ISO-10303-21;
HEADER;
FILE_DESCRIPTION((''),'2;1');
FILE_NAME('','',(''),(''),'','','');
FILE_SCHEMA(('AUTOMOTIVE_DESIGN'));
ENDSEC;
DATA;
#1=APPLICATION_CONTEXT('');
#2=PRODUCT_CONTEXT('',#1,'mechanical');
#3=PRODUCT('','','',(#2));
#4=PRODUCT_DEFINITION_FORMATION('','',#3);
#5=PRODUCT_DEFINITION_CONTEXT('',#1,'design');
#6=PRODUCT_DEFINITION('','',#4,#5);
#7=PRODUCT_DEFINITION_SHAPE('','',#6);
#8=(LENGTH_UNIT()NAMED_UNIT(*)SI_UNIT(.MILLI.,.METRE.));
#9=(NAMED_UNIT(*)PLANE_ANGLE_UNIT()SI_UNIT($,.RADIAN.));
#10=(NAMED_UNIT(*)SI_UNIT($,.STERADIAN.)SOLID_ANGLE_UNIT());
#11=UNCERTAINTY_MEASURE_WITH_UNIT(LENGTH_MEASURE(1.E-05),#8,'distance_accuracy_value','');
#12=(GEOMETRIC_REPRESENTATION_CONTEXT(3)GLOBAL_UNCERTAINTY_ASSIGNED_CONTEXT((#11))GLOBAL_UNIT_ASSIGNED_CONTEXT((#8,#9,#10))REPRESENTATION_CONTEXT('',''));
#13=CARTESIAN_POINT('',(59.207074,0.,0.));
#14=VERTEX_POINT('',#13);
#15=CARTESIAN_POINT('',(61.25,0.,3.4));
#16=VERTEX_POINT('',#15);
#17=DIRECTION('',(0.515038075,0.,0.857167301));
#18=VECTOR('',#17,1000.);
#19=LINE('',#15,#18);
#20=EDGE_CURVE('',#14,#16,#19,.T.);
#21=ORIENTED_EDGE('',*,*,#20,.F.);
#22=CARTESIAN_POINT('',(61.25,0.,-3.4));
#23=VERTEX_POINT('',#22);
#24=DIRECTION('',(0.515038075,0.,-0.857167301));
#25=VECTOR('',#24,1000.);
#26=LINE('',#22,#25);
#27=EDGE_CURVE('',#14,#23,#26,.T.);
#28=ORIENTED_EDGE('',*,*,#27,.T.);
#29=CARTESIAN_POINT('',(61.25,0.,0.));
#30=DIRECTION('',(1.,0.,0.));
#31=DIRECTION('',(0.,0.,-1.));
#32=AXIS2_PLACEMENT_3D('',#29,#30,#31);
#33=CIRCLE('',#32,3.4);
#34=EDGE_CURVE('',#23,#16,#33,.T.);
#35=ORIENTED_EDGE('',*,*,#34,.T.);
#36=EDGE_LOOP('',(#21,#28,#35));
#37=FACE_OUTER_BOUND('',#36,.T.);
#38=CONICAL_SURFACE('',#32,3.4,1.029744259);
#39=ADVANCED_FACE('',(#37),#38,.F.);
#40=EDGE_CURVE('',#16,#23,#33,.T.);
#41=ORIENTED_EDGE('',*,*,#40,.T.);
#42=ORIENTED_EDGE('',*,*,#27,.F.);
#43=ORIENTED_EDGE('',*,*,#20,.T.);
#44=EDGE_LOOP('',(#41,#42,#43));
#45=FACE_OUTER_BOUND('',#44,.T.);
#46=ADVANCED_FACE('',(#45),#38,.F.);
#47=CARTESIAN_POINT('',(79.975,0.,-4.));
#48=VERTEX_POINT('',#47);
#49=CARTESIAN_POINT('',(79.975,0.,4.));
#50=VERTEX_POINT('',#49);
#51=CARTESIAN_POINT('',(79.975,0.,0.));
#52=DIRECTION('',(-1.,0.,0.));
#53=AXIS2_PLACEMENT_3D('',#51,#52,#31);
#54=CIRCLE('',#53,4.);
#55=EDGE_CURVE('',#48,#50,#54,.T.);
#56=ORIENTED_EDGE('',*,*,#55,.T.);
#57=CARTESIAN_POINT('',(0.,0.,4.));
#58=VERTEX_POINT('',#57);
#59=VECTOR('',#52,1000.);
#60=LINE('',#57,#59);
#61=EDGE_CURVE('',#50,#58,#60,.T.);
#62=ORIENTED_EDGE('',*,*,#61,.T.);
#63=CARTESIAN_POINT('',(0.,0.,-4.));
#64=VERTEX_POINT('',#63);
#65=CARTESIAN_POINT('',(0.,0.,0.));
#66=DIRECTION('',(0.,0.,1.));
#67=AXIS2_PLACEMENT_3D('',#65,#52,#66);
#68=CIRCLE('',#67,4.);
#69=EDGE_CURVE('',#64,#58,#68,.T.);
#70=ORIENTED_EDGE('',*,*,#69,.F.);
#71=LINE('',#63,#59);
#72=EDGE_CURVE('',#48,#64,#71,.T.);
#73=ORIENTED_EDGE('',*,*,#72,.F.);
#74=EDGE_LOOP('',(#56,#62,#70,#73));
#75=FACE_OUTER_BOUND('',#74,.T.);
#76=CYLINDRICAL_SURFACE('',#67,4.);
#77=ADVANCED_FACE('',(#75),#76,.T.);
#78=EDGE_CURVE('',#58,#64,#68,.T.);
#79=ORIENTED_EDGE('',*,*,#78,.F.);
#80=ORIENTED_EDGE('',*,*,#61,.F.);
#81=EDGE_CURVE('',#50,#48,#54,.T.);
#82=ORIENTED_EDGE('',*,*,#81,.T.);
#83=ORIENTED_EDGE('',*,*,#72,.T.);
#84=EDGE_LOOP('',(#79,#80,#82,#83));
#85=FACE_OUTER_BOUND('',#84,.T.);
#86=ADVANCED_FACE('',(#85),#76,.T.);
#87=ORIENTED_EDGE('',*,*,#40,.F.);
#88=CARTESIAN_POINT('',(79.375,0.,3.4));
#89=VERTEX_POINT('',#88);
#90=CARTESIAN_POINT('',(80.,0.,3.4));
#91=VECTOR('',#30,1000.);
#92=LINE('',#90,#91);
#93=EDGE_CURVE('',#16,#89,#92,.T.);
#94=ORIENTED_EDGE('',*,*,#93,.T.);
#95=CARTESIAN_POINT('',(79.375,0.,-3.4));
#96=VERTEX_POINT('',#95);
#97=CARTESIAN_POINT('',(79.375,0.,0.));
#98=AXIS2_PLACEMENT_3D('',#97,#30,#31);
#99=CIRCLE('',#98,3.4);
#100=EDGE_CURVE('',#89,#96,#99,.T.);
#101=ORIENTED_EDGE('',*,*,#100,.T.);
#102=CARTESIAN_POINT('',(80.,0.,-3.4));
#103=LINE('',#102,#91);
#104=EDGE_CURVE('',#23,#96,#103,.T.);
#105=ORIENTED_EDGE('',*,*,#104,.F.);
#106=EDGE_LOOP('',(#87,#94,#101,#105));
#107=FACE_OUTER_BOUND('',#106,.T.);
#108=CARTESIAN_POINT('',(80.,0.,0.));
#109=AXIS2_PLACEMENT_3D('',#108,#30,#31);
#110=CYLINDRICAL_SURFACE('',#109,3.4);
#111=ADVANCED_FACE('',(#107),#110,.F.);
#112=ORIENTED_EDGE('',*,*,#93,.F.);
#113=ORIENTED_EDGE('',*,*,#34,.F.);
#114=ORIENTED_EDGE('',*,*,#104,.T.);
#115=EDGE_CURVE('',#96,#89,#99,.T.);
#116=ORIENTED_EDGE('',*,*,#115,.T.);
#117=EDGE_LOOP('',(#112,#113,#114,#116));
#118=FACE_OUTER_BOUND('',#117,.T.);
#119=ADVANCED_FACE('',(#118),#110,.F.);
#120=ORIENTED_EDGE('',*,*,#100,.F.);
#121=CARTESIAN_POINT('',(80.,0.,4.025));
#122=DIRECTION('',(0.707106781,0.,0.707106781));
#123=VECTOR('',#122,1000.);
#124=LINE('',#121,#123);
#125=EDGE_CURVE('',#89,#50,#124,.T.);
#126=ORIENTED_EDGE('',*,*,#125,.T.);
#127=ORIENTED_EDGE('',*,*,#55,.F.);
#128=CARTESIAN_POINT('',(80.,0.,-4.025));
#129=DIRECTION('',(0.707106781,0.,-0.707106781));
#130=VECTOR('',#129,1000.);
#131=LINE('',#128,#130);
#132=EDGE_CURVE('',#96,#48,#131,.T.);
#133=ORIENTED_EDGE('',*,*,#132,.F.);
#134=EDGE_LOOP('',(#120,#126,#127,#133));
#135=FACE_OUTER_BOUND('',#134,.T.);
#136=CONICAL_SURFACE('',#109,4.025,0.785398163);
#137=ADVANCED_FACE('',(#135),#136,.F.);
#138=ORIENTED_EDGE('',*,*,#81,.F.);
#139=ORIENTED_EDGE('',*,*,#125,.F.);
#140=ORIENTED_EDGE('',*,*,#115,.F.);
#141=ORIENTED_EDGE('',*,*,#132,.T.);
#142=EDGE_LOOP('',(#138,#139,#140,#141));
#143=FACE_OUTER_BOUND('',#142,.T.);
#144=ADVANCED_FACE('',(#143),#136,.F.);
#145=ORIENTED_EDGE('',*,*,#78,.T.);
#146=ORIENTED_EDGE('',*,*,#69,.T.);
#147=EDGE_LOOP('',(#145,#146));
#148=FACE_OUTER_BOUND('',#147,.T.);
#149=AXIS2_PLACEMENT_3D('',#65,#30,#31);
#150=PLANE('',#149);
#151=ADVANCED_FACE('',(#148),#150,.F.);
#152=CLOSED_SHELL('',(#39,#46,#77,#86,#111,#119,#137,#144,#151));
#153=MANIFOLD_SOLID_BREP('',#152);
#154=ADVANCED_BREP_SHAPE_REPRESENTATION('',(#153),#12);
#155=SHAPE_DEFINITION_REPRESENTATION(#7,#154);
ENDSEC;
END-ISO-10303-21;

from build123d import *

# Parameters (mm, degrees)
SKETCH1_W                   = 80
SKETCH1_H                   = 4
M8_TAPPED_HOLE1_D           = 6.8
M8_TAPPED_HOLE1_DEPTH       = 18.75
M8_TAPPED_HOLE1_CSINK_D     = 8.05
M8_TAPPED_HOLE1_CSINK_ANGLE = 90
M8_TAPPED_HOLE1_TIP         = 2.042926105


with BuildPart() as part:
    # Sketch1 → Revolve1 (revolve)
    with BuildSketch(Plane.XY, mode=Mode.PRIVATE) as revolve1_sk:
        with Locations((40, 2)):
            Rectangle(SKETCH1_W, SKETCH1_H)
    revolve(revolve1_sk.sketch.rotate(Axis((0, 0, 0), (1, 0, 0)), 90), axis=Axis((0, 0, 0), (1, 0, 0)))

    # M8 Tapped Hole1
    with Locations(Plane(origin=(80, 0, 0), x_dir=(0, 0, 1), z_dir=(1, 0, 0))):
        with Locations((0, 0)):
            CounterSinkHole(M8_TAPPED_HOLE1_D / 2, M8_TAPPED_HOLE1_CSINK_D / 2, depth=M8_TAPPED_HOLE1_DEPTH, counter_sink_angle=M8_TAPPED_HOLE1_CSINK_ANGLE)
            with Locations((0, 0, -(M8_TAPPED_HOLE1_DEPTH + M8_TAPPED_HOLE1_TIP / 2))):  # 118° drill point
                Cone(0, M8_TAPPED_HOLE1_D / 2, M8_TAPPED_HOLE1_TIP, mode=Mode.SUBTRACT)


solid = part.part
